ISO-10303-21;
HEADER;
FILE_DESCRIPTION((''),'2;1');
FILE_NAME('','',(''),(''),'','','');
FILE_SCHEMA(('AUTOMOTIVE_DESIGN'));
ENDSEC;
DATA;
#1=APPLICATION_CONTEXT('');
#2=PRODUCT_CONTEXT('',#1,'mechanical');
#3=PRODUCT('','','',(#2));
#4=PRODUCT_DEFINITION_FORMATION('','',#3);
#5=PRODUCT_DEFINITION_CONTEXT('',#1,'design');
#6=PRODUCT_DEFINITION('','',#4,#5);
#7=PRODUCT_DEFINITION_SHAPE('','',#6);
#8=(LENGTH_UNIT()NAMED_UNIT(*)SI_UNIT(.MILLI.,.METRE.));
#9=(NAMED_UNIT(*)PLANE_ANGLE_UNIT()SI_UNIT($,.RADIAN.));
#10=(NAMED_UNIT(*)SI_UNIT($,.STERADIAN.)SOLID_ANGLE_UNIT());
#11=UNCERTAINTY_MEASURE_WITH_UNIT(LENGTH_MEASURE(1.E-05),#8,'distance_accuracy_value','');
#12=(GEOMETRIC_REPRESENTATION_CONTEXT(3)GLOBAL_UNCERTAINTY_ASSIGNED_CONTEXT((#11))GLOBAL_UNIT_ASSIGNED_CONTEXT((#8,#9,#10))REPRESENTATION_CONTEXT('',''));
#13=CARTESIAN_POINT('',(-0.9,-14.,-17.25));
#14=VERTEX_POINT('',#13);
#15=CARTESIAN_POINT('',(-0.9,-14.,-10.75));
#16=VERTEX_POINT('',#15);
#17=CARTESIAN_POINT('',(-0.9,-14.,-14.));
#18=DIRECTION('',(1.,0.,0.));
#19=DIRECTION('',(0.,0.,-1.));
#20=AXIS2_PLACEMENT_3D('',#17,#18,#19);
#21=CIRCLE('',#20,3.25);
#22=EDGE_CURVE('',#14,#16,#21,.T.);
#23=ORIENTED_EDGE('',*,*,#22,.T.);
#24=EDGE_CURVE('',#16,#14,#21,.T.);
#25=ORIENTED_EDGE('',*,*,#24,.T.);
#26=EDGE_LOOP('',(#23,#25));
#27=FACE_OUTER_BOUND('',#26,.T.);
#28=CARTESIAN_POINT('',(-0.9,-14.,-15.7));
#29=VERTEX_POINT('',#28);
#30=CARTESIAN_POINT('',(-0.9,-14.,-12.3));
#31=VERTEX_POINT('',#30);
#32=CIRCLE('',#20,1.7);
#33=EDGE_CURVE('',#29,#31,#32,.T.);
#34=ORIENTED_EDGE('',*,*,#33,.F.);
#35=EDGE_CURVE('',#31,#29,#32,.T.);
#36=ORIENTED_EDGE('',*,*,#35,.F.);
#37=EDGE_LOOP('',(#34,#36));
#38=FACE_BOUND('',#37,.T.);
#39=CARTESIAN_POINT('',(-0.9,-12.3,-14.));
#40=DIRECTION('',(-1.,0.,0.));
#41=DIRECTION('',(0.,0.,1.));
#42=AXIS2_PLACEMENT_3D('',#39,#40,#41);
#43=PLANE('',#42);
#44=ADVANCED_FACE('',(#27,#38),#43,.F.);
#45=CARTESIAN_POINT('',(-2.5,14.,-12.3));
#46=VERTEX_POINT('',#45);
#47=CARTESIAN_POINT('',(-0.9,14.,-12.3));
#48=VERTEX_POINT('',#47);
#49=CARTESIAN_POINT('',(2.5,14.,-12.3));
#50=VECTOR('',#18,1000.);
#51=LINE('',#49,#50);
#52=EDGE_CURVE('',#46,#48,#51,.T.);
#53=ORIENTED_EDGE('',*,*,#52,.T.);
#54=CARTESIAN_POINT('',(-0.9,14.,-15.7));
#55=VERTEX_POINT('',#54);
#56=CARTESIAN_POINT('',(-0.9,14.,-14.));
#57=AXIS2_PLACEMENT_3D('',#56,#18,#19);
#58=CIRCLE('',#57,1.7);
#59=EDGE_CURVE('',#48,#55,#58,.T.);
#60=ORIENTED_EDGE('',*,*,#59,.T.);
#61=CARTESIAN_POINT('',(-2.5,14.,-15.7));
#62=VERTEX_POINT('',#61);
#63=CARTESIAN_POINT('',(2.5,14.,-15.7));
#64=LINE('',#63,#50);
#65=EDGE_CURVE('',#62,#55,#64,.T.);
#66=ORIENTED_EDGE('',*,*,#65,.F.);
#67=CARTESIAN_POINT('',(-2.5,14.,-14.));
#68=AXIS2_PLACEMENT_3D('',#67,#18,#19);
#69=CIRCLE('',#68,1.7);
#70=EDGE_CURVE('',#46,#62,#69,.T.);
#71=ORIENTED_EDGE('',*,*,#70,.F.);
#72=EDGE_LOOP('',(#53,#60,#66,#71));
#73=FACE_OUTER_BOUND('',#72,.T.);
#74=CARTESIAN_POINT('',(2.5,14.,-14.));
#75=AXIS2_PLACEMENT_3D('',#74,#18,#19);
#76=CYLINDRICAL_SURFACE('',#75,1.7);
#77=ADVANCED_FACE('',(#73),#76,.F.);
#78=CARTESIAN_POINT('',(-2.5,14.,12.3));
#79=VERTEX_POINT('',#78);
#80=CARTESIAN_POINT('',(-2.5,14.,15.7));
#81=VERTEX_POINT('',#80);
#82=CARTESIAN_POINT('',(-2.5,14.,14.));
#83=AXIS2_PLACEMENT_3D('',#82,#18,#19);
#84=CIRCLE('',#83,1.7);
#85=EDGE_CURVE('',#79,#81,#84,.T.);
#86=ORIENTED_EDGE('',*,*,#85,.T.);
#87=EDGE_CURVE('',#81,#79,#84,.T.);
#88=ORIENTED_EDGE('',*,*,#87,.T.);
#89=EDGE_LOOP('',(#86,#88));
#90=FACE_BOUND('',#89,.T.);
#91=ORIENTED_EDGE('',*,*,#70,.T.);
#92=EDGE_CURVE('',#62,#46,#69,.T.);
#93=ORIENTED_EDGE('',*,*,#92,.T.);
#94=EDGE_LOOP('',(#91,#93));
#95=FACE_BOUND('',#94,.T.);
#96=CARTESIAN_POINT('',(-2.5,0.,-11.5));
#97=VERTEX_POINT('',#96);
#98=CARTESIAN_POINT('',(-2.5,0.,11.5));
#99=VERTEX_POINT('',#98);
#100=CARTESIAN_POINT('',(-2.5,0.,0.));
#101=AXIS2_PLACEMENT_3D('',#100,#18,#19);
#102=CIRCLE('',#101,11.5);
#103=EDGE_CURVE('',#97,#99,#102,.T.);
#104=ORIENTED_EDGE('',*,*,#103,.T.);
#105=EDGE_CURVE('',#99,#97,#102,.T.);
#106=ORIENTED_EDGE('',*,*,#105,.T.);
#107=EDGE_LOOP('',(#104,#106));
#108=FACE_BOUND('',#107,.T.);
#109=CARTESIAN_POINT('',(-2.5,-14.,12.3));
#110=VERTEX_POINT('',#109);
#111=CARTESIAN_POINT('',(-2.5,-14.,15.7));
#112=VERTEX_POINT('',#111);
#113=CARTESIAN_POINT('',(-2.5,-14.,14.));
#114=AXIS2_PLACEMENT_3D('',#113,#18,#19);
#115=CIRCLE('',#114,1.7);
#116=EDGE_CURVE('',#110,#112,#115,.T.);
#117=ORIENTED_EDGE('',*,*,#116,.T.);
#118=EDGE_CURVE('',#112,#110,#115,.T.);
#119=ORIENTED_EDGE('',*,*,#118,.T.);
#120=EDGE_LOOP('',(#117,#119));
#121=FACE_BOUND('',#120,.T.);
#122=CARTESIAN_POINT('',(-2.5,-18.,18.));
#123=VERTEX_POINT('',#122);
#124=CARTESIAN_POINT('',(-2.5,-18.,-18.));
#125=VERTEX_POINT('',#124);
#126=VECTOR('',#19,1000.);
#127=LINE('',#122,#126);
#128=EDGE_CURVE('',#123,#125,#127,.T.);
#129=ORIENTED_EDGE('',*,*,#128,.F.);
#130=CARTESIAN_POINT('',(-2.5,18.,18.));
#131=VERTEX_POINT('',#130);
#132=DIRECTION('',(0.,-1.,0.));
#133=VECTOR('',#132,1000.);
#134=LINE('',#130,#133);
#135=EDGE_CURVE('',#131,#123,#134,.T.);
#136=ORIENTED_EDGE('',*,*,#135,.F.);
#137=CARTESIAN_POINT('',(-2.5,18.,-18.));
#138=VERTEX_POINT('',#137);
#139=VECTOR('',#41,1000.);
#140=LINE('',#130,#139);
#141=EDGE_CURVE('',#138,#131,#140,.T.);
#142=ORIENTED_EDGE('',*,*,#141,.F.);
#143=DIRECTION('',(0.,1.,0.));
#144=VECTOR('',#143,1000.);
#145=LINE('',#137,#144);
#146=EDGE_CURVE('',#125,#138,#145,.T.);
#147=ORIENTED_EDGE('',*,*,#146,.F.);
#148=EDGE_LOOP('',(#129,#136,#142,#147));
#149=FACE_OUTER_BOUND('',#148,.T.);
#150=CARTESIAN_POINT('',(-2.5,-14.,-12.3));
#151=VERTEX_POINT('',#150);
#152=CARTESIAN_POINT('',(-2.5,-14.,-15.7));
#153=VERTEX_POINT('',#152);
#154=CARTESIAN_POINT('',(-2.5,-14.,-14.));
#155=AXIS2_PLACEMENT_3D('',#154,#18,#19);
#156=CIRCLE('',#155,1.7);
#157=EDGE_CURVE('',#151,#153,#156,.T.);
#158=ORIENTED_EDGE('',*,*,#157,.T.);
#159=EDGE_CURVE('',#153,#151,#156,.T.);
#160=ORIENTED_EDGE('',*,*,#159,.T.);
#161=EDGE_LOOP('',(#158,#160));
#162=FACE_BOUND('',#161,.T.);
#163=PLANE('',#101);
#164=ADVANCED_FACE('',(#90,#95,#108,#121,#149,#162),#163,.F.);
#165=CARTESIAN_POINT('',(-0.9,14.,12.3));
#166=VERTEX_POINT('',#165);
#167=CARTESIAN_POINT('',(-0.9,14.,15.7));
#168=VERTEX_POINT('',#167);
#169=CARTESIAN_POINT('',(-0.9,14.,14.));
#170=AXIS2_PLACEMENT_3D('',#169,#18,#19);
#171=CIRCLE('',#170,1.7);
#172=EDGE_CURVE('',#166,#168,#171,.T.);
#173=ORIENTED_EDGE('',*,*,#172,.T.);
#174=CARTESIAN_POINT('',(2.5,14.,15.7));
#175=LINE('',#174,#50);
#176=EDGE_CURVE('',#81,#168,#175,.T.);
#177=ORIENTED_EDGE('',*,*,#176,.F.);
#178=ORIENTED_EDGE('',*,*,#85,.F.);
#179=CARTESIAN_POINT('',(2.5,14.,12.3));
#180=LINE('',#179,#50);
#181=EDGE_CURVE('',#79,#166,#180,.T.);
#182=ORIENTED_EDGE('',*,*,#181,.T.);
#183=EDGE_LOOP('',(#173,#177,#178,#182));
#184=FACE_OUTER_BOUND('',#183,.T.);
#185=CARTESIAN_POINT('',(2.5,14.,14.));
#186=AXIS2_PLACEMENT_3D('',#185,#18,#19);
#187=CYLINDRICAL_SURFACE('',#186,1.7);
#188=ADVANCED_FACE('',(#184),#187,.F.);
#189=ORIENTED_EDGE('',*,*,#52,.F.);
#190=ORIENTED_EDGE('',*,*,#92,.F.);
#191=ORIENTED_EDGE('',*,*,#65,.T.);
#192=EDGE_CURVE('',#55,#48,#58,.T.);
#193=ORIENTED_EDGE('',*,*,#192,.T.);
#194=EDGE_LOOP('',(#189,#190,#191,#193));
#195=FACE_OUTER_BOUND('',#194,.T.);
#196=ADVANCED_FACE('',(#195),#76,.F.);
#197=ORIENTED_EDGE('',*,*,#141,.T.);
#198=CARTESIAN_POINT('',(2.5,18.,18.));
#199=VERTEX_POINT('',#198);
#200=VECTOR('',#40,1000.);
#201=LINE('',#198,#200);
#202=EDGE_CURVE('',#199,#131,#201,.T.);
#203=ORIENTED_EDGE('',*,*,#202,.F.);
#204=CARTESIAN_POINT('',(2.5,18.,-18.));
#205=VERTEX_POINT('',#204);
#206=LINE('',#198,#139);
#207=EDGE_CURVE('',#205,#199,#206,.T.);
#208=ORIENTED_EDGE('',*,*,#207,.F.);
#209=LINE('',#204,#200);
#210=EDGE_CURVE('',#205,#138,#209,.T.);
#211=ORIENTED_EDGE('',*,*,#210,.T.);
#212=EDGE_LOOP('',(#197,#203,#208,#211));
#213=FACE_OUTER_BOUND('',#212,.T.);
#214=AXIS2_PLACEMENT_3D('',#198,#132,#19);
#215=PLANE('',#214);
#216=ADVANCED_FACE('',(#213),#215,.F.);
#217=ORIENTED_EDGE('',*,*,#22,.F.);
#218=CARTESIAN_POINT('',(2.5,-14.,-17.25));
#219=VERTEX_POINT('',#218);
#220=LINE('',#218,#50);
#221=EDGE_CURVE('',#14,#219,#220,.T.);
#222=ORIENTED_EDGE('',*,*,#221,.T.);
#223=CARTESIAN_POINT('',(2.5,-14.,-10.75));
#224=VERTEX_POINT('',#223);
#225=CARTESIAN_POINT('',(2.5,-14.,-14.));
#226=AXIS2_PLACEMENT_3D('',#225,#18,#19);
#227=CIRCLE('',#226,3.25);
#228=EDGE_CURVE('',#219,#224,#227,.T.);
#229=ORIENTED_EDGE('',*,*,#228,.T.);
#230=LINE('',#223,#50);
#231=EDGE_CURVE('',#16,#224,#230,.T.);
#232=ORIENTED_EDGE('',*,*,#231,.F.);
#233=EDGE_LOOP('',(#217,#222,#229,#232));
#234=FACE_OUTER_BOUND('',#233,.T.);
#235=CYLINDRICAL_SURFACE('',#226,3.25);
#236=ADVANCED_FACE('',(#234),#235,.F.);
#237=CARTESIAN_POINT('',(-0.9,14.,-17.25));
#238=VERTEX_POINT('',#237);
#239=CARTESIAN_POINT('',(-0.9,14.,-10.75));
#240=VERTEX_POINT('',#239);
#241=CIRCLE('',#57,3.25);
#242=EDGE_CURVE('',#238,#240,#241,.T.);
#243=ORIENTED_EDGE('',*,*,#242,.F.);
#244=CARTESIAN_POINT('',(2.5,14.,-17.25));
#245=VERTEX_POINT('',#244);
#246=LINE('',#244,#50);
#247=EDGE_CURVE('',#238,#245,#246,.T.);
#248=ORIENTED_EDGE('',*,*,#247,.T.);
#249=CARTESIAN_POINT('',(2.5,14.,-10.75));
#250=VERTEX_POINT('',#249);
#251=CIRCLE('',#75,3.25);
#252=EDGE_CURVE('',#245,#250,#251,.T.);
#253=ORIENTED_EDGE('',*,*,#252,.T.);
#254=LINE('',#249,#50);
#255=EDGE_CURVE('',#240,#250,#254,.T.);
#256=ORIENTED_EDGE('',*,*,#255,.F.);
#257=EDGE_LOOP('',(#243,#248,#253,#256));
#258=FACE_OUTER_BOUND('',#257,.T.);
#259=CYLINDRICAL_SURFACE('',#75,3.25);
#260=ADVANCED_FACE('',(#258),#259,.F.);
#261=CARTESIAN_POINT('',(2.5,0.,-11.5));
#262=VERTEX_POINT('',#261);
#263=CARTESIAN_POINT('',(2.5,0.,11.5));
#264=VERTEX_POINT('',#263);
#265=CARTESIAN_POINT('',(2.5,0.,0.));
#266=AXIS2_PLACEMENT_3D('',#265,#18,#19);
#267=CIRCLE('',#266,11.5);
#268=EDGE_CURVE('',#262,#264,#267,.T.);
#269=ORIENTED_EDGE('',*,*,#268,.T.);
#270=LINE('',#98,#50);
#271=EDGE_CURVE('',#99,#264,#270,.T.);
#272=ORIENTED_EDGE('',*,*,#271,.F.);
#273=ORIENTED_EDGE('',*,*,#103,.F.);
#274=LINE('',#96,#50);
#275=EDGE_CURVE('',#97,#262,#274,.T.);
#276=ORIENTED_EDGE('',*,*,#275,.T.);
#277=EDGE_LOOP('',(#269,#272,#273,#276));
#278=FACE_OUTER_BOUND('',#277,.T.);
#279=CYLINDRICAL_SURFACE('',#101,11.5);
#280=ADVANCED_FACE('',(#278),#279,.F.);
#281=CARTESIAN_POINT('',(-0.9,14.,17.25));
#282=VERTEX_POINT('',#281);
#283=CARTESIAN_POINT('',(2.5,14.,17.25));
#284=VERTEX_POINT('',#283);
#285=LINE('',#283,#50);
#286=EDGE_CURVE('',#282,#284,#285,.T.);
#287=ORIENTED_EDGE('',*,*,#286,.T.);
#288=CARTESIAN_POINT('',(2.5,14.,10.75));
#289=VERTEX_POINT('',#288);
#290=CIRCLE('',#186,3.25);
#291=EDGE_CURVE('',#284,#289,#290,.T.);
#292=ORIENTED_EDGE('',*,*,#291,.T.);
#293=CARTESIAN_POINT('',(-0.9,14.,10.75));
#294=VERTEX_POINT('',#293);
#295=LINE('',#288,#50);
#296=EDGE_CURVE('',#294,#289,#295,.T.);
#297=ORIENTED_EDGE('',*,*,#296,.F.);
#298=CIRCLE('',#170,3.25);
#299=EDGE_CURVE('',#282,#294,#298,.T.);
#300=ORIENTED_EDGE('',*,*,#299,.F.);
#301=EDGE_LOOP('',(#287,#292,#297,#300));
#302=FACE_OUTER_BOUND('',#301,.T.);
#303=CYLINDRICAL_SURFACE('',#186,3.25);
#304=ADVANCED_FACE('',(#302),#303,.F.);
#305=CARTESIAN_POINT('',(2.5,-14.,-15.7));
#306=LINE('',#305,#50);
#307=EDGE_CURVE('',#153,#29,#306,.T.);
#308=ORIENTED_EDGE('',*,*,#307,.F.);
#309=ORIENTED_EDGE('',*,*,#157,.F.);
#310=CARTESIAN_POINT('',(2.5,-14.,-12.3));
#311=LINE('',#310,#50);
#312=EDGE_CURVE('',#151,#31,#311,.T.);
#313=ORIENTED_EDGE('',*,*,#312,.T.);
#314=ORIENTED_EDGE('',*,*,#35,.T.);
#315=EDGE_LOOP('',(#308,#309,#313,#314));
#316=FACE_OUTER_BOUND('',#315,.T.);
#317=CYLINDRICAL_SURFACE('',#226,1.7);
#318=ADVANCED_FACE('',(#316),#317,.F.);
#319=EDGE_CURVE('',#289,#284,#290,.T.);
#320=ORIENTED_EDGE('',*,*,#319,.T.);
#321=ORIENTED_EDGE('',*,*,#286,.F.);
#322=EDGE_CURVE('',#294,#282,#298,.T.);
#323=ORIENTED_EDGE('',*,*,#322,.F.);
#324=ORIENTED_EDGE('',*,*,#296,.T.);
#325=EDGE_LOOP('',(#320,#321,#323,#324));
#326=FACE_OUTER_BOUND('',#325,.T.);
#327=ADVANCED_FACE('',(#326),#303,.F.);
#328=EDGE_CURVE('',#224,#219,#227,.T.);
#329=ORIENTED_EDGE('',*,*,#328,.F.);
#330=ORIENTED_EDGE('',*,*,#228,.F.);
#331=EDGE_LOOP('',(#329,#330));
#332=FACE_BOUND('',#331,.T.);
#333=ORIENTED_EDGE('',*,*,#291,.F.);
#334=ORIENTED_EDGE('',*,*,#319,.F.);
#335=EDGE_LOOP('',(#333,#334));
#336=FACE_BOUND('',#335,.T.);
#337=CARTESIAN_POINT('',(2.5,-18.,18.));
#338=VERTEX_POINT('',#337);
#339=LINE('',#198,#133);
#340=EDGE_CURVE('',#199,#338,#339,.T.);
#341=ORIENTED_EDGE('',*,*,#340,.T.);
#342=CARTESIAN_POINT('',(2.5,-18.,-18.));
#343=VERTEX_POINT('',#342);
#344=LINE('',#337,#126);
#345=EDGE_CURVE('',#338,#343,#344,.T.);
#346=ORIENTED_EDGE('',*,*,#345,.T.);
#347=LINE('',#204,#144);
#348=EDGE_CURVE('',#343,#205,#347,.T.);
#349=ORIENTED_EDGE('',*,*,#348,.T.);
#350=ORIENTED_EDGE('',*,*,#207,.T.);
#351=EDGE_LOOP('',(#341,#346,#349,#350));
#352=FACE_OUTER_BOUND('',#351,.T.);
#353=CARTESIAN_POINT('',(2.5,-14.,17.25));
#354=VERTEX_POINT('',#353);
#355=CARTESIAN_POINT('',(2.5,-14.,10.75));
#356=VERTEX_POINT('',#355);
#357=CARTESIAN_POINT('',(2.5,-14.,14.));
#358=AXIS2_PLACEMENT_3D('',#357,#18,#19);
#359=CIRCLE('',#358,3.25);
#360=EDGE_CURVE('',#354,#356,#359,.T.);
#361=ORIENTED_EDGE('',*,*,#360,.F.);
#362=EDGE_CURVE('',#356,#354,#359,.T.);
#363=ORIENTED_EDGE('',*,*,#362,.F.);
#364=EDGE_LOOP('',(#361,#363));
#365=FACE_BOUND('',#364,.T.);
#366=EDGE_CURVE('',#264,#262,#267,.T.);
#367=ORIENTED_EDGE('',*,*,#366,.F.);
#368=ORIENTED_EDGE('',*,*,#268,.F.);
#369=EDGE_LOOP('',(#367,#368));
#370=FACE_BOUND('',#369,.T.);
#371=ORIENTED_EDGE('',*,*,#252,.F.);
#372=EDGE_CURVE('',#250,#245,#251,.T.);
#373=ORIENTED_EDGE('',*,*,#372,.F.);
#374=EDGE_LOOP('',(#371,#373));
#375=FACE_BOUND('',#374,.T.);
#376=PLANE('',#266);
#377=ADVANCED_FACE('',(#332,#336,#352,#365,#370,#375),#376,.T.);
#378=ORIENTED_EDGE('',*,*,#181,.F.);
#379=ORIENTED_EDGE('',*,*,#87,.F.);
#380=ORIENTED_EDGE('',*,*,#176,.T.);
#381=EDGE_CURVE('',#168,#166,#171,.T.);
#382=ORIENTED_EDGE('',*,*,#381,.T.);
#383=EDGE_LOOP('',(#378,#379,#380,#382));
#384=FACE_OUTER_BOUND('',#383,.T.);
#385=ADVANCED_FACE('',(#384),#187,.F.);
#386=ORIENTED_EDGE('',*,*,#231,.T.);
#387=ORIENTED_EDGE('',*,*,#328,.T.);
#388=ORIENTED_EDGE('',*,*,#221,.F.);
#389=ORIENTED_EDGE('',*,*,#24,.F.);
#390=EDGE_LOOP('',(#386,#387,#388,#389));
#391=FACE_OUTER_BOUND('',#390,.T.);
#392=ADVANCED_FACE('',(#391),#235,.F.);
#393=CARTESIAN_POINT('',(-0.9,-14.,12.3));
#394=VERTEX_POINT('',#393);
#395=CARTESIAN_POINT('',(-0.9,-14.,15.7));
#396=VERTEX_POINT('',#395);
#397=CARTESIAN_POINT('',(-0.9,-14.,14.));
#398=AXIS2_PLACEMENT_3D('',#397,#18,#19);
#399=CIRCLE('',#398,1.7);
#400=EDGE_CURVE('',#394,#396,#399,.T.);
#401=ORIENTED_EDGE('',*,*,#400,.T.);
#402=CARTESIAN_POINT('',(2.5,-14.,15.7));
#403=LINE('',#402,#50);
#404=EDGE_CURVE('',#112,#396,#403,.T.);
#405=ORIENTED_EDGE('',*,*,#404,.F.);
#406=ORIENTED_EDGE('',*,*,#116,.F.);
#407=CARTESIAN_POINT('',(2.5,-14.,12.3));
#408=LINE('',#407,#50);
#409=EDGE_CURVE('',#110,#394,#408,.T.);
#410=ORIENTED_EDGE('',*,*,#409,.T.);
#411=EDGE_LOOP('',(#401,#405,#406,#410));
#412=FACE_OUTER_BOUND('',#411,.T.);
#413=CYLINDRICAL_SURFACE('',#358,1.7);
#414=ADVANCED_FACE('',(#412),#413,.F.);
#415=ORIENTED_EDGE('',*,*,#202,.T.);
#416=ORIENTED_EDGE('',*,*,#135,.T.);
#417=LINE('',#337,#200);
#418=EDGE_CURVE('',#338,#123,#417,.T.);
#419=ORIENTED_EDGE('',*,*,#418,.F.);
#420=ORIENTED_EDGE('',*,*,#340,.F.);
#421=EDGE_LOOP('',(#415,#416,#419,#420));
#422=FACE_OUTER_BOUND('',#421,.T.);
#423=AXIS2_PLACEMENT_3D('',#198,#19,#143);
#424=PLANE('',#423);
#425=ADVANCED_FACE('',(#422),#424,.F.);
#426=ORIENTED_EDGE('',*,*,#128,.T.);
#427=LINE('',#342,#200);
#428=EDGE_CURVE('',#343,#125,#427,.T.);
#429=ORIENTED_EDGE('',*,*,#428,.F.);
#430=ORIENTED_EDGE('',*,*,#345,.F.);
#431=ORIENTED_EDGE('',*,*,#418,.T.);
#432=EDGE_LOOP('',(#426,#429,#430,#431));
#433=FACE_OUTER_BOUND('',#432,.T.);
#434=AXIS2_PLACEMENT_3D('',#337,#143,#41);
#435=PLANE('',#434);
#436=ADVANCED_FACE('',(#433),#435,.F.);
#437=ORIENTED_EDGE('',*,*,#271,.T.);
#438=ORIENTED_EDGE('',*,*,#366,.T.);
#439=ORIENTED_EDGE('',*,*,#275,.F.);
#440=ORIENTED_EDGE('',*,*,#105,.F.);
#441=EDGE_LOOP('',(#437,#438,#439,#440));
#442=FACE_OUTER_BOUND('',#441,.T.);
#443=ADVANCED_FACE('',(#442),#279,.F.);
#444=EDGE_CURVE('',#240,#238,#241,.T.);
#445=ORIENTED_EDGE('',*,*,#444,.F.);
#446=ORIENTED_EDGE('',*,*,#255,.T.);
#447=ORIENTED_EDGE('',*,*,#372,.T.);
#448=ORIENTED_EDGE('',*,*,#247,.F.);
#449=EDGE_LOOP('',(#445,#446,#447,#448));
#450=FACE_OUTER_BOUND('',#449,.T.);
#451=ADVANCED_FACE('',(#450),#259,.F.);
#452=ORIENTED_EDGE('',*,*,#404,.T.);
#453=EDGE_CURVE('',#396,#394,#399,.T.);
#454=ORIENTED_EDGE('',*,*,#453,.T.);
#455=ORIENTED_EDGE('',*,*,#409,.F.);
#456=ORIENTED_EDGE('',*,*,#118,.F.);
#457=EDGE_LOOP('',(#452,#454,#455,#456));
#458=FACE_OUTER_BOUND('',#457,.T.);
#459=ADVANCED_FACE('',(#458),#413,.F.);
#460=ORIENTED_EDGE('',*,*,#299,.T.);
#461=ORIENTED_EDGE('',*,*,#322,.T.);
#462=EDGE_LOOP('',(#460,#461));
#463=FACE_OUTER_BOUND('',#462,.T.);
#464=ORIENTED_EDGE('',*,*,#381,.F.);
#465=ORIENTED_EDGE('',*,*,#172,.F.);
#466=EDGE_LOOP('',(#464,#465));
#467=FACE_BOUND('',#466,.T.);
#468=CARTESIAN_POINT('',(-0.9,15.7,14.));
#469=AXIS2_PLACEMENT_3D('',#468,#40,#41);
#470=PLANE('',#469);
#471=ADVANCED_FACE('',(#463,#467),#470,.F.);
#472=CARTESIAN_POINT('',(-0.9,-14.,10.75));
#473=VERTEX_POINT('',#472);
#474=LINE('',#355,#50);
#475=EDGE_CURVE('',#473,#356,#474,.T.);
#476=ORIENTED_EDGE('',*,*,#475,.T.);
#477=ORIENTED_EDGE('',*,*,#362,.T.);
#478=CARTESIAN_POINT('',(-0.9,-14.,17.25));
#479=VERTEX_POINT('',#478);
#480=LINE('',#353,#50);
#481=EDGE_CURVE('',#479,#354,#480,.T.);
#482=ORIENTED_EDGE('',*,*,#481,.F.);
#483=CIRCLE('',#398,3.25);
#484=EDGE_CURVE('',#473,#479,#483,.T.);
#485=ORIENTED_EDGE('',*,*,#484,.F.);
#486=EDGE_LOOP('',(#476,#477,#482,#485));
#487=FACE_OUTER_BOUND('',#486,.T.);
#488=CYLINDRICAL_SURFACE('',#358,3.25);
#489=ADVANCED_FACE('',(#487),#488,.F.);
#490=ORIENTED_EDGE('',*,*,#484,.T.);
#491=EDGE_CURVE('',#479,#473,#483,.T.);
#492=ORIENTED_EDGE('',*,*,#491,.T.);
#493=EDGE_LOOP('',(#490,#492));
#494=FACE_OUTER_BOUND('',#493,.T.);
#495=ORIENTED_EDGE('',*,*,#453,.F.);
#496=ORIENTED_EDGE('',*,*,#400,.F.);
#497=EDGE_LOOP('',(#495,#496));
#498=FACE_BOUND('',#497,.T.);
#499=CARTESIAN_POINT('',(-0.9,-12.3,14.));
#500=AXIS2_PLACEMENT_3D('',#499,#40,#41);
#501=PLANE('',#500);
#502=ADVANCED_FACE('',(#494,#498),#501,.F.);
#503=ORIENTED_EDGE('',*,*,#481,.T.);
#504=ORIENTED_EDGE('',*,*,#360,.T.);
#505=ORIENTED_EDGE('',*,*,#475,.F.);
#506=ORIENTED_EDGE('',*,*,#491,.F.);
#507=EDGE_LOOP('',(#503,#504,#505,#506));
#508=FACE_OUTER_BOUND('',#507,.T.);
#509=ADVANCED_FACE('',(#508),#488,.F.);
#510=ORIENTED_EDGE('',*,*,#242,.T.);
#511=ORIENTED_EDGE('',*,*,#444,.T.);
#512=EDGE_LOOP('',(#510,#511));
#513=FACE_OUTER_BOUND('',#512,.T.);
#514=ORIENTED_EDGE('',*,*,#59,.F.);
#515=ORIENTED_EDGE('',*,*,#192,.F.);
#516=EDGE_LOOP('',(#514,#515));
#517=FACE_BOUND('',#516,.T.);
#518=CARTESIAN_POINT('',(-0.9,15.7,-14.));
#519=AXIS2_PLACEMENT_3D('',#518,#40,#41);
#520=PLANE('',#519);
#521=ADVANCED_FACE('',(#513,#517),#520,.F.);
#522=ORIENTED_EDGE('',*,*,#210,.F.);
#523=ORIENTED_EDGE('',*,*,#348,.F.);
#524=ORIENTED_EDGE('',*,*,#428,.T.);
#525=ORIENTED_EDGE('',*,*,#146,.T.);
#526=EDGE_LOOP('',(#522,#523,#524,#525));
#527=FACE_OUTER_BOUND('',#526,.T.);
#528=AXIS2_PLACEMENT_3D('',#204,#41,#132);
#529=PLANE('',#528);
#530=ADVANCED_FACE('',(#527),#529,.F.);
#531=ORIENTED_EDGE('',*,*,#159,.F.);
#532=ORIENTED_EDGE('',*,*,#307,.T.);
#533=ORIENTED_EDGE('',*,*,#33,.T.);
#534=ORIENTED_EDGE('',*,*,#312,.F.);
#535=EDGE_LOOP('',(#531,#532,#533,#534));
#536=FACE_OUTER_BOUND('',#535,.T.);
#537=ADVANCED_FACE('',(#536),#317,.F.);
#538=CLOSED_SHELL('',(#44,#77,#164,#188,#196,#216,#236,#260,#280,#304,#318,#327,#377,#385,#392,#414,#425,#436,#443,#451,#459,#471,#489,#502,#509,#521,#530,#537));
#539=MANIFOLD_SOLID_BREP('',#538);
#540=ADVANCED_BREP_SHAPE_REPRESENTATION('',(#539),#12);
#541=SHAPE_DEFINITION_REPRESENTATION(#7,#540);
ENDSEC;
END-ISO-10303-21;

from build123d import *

# Parameters (mm, degrees)
SKETCH1_W                                           = 36
SKETCH1_H                                           = 36
BOSS_EXTRUDE1_DEPTH                                 = 2.5
CBORE_FOR_M3_HEX_SOCKET_HEAD_CAP_SCREW1_D           = 3.4
CBORE_FOR_M3_HEX_SOCKET_HEAD_CAP_SCREW1_CBORE_D     = 6.5
CBORE_FOR_M3_HEX_SOCKET_HEAD_CAP_SCREW1_CBORE_DEPTH = 3.4
SKETCH5_R                                           = 11.5
CUT_EXTRUDE2_DEPTH                                  = 26.942243542


with BuildPart() as part:
    # Sketch1 → Boss-Extrude1 (new, symmetric)
    with BuildSketch(Plane(origin=(0, 0, 0), x_dir=(0, 0, -1), z_dir=(1, 0, 0))):
        Rectangle(SKETCH1_W, SKETCH1_H)
    extrude(amount=BOSS_EXTRUDE1_DEPTH, both=True)

    # CBORE for M3 Hex Socket Head Cap Screw1 (through all)
    with Locations(Plane(origin=(2.5, 0, 0), x_dir=(0, 0, -1), z_dir=(1, 0, 0))):
        with Locations((-14, 14), (14, 14), (-14, -14), (14, -14)):
            CounterBoreHole(CBORE_FOR_M3_HEX_SOCKET_HEAD_CAP_SCREW1_D / 2, CBORE_FOR_M3_HEX_SOCKET_HEAD_CAP_SCREW1_CBORE_D / 2, CBORE_FOR_M3_HEX_SOCKET_HEAD_CAP_SCREW1_CBORE_DEPTH)

    # Sketch5 → Cut-Extrude2 (cut, through all)
    with BuildSketch(Plane(origin=(2.5, 0, 0), x_dir=(0, 0, -1), z_dir=(1, 0, 0))):
        Circle(SKETCH5_R)
    extrude(amount=-CUT_EXTRUDE2_DEPTH, mode=Mode.SUBTRACT)


solid = part.part
